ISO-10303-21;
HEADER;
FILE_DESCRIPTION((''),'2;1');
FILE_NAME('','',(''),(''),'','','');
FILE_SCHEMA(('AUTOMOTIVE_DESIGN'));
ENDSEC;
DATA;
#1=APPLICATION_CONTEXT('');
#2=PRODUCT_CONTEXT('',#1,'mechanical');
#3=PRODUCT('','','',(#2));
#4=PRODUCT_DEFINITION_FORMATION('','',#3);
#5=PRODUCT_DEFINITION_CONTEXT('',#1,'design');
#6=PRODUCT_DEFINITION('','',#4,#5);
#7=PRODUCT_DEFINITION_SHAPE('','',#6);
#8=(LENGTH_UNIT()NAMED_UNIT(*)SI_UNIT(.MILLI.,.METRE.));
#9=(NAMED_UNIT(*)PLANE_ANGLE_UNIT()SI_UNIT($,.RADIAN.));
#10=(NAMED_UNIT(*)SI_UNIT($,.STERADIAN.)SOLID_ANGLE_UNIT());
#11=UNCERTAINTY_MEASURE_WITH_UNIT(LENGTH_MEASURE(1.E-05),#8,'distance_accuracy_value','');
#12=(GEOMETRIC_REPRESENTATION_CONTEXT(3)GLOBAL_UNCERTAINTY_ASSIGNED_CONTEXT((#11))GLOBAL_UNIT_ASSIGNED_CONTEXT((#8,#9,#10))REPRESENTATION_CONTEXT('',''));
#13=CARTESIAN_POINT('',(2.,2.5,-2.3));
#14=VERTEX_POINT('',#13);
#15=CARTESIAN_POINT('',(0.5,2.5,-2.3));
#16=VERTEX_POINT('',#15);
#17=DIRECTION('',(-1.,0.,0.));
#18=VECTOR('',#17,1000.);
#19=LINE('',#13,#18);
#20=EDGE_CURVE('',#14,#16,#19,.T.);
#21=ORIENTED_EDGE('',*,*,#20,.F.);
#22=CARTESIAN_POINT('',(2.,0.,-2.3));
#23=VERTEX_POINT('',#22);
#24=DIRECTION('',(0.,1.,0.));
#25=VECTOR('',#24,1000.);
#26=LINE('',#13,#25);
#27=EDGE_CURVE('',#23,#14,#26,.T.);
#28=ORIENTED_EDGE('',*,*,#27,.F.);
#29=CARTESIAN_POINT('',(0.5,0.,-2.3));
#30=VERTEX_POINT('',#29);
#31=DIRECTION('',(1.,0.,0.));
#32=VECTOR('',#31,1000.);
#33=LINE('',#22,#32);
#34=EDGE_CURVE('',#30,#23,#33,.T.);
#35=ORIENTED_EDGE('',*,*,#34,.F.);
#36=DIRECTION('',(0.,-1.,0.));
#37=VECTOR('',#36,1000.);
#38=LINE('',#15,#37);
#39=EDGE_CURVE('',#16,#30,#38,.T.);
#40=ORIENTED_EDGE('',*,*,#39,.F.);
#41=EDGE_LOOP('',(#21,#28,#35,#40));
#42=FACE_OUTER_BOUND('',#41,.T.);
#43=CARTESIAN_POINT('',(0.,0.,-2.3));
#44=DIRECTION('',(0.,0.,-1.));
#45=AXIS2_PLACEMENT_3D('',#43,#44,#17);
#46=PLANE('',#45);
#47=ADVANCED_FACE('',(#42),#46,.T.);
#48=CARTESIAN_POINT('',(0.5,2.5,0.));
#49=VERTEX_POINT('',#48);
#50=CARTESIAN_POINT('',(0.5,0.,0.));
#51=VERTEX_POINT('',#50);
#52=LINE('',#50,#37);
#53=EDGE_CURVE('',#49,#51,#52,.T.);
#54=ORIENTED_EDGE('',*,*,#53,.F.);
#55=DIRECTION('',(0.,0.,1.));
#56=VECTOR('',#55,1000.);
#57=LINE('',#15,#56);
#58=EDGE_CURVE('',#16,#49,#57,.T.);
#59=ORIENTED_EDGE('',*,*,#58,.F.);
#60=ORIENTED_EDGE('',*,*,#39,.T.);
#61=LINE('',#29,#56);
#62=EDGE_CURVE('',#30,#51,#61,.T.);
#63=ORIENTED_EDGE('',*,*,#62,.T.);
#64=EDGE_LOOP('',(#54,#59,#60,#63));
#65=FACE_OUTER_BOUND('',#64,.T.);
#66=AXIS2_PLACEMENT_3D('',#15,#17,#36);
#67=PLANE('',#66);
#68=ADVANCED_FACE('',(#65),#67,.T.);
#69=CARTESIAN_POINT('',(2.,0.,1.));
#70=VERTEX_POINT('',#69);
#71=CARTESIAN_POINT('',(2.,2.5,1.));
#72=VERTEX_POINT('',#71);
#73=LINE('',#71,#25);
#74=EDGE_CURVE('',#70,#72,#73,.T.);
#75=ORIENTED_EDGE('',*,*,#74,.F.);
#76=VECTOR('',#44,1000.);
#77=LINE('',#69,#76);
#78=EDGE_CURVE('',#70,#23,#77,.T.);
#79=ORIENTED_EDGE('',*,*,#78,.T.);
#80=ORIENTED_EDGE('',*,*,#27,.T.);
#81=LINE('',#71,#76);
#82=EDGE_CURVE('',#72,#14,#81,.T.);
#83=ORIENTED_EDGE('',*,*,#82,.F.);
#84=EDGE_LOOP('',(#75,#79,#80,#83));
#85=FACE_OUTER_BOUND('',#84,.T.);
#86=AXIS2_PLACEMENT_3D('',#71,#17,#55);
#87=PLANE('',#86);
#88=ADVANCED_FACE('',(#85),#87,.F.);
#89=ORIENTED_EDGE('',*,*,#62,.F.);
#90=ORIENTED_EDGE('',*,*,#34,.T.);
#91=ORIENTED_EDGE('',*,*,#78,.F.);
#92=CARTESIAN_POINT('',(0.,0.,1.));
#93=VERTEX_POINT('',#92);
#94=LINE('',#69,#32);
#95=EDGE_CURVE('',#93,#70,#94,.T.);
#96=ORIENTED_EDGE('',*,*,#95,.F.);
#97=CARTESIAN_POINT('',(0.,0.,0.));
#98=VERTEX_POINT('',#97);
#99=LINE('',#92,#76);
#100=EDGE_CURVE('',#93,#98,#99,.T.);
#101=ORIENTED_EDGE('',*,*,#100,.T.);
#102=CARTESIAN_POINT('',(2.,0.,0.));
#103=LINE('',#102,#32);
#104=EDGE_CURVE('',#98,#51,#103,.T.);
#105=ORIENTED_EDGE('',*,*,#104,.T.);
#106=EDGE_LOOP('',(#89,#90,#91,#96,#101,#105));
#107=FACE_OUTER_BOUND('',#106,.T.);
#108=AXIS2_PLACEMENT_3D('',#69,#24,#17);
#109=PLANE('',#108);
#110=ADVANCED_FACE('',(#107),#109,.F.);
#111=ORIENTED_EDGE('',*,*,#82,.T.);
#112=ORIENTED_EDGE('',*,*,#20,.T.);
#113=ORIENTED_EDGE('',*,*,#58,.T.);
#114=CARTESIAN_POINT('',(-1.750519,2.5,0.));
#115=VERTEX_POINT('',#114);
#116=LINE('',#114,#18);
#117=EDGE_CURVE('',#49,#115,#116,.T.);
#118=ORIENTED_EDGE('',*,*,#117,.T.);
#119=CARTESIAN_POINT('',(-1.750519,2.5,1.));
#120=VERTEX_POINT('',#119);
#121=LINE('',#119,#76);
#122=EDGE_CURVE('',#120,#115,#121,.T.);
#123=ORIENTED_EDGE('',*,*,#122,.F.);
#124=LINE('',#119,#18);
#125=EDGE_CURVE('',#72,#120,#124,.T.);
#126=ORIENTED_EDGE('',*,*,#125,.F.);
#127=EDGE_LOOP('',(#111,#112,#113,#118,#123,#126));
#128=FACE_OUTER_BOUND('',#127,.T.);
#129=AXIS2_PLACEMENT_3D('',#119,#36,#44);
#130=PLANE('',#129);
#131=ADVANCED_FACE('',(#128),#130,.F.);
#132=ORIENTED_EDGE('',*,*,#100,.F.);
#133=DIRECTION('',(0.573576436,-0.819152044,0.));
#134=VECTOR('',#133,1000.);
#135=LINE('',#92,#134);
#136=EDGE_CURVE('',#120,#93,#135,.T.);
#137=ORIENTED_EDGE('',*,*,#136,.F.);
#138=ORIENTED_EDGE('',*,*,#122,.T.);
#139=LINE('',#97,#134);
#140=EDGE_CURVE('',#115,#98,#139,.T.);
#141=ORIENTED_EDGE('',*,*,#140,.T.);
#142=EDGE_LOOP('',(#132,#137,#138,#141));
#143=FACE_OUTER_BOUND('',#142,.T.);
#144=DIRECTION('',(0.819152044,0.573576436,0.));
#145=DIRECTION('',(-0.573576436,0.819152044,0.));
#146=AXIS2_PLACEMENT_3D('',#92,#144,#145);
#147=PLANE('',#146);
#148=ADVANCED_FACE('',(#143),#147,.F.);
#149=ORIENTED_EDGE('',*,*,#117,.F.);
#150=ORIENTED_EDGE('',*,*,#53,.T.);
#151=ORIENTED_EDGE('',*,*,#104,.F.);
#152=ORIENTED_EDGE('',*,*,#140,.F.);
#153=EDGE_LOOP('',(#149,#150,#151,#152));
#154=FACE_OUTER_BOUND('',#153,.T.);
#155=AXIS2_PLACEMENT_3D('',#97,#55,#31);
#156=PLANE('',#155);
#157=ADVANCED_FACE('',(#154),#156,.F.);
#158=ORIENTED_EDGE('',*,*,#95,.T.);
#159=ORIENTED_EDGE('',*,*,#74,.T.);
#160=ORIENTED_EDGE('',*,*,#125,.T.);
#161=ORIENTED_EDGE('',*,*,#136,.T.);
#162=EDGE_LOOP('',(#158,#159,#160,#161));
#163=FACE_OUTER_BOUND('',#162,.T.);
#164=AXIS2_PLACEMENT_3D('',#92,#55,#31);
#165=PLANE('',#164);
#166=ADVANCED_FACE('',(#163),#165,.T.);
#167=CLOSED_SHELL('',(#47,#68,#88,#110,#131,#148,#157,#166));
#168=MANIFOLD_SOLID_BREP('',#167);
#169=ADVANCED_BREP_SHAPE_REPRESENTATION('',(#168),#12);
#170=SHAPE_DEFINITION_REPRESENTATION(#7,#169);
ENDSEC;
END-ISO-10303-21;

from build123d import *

# Parameters (mm, degrees)
BOSS_EXTRUDE1_DEPTH = 1
SKETCH2_W           = 1.5
SKETCH2_H           = 2.5
BOSS_EXTRUDE2_DEPTH = 3.3


with BuildPart() as part:
    # Sketch1 → Boss-Extrude1 (new body)
    with BuildSketch(Plane.XY):
        Polygon((0, 0), (-1.750518846, 2.5), (2, 2.5), (2, 0), align=None)
    extrude(amount=BOSS_EXTRUDE1_DEPTH)

    # Sketch2 → Boss-Extrude2 (add)
    with BuildSketch(Plane.XY.offset(1)):
        with Locations((1.25, 1.25)):
            Rectangle(SKETCH2_W, SKETCH2_H)
    extrude(amount=-BOSS_EXTRUDE2_DEPTH)


solid = part.part
